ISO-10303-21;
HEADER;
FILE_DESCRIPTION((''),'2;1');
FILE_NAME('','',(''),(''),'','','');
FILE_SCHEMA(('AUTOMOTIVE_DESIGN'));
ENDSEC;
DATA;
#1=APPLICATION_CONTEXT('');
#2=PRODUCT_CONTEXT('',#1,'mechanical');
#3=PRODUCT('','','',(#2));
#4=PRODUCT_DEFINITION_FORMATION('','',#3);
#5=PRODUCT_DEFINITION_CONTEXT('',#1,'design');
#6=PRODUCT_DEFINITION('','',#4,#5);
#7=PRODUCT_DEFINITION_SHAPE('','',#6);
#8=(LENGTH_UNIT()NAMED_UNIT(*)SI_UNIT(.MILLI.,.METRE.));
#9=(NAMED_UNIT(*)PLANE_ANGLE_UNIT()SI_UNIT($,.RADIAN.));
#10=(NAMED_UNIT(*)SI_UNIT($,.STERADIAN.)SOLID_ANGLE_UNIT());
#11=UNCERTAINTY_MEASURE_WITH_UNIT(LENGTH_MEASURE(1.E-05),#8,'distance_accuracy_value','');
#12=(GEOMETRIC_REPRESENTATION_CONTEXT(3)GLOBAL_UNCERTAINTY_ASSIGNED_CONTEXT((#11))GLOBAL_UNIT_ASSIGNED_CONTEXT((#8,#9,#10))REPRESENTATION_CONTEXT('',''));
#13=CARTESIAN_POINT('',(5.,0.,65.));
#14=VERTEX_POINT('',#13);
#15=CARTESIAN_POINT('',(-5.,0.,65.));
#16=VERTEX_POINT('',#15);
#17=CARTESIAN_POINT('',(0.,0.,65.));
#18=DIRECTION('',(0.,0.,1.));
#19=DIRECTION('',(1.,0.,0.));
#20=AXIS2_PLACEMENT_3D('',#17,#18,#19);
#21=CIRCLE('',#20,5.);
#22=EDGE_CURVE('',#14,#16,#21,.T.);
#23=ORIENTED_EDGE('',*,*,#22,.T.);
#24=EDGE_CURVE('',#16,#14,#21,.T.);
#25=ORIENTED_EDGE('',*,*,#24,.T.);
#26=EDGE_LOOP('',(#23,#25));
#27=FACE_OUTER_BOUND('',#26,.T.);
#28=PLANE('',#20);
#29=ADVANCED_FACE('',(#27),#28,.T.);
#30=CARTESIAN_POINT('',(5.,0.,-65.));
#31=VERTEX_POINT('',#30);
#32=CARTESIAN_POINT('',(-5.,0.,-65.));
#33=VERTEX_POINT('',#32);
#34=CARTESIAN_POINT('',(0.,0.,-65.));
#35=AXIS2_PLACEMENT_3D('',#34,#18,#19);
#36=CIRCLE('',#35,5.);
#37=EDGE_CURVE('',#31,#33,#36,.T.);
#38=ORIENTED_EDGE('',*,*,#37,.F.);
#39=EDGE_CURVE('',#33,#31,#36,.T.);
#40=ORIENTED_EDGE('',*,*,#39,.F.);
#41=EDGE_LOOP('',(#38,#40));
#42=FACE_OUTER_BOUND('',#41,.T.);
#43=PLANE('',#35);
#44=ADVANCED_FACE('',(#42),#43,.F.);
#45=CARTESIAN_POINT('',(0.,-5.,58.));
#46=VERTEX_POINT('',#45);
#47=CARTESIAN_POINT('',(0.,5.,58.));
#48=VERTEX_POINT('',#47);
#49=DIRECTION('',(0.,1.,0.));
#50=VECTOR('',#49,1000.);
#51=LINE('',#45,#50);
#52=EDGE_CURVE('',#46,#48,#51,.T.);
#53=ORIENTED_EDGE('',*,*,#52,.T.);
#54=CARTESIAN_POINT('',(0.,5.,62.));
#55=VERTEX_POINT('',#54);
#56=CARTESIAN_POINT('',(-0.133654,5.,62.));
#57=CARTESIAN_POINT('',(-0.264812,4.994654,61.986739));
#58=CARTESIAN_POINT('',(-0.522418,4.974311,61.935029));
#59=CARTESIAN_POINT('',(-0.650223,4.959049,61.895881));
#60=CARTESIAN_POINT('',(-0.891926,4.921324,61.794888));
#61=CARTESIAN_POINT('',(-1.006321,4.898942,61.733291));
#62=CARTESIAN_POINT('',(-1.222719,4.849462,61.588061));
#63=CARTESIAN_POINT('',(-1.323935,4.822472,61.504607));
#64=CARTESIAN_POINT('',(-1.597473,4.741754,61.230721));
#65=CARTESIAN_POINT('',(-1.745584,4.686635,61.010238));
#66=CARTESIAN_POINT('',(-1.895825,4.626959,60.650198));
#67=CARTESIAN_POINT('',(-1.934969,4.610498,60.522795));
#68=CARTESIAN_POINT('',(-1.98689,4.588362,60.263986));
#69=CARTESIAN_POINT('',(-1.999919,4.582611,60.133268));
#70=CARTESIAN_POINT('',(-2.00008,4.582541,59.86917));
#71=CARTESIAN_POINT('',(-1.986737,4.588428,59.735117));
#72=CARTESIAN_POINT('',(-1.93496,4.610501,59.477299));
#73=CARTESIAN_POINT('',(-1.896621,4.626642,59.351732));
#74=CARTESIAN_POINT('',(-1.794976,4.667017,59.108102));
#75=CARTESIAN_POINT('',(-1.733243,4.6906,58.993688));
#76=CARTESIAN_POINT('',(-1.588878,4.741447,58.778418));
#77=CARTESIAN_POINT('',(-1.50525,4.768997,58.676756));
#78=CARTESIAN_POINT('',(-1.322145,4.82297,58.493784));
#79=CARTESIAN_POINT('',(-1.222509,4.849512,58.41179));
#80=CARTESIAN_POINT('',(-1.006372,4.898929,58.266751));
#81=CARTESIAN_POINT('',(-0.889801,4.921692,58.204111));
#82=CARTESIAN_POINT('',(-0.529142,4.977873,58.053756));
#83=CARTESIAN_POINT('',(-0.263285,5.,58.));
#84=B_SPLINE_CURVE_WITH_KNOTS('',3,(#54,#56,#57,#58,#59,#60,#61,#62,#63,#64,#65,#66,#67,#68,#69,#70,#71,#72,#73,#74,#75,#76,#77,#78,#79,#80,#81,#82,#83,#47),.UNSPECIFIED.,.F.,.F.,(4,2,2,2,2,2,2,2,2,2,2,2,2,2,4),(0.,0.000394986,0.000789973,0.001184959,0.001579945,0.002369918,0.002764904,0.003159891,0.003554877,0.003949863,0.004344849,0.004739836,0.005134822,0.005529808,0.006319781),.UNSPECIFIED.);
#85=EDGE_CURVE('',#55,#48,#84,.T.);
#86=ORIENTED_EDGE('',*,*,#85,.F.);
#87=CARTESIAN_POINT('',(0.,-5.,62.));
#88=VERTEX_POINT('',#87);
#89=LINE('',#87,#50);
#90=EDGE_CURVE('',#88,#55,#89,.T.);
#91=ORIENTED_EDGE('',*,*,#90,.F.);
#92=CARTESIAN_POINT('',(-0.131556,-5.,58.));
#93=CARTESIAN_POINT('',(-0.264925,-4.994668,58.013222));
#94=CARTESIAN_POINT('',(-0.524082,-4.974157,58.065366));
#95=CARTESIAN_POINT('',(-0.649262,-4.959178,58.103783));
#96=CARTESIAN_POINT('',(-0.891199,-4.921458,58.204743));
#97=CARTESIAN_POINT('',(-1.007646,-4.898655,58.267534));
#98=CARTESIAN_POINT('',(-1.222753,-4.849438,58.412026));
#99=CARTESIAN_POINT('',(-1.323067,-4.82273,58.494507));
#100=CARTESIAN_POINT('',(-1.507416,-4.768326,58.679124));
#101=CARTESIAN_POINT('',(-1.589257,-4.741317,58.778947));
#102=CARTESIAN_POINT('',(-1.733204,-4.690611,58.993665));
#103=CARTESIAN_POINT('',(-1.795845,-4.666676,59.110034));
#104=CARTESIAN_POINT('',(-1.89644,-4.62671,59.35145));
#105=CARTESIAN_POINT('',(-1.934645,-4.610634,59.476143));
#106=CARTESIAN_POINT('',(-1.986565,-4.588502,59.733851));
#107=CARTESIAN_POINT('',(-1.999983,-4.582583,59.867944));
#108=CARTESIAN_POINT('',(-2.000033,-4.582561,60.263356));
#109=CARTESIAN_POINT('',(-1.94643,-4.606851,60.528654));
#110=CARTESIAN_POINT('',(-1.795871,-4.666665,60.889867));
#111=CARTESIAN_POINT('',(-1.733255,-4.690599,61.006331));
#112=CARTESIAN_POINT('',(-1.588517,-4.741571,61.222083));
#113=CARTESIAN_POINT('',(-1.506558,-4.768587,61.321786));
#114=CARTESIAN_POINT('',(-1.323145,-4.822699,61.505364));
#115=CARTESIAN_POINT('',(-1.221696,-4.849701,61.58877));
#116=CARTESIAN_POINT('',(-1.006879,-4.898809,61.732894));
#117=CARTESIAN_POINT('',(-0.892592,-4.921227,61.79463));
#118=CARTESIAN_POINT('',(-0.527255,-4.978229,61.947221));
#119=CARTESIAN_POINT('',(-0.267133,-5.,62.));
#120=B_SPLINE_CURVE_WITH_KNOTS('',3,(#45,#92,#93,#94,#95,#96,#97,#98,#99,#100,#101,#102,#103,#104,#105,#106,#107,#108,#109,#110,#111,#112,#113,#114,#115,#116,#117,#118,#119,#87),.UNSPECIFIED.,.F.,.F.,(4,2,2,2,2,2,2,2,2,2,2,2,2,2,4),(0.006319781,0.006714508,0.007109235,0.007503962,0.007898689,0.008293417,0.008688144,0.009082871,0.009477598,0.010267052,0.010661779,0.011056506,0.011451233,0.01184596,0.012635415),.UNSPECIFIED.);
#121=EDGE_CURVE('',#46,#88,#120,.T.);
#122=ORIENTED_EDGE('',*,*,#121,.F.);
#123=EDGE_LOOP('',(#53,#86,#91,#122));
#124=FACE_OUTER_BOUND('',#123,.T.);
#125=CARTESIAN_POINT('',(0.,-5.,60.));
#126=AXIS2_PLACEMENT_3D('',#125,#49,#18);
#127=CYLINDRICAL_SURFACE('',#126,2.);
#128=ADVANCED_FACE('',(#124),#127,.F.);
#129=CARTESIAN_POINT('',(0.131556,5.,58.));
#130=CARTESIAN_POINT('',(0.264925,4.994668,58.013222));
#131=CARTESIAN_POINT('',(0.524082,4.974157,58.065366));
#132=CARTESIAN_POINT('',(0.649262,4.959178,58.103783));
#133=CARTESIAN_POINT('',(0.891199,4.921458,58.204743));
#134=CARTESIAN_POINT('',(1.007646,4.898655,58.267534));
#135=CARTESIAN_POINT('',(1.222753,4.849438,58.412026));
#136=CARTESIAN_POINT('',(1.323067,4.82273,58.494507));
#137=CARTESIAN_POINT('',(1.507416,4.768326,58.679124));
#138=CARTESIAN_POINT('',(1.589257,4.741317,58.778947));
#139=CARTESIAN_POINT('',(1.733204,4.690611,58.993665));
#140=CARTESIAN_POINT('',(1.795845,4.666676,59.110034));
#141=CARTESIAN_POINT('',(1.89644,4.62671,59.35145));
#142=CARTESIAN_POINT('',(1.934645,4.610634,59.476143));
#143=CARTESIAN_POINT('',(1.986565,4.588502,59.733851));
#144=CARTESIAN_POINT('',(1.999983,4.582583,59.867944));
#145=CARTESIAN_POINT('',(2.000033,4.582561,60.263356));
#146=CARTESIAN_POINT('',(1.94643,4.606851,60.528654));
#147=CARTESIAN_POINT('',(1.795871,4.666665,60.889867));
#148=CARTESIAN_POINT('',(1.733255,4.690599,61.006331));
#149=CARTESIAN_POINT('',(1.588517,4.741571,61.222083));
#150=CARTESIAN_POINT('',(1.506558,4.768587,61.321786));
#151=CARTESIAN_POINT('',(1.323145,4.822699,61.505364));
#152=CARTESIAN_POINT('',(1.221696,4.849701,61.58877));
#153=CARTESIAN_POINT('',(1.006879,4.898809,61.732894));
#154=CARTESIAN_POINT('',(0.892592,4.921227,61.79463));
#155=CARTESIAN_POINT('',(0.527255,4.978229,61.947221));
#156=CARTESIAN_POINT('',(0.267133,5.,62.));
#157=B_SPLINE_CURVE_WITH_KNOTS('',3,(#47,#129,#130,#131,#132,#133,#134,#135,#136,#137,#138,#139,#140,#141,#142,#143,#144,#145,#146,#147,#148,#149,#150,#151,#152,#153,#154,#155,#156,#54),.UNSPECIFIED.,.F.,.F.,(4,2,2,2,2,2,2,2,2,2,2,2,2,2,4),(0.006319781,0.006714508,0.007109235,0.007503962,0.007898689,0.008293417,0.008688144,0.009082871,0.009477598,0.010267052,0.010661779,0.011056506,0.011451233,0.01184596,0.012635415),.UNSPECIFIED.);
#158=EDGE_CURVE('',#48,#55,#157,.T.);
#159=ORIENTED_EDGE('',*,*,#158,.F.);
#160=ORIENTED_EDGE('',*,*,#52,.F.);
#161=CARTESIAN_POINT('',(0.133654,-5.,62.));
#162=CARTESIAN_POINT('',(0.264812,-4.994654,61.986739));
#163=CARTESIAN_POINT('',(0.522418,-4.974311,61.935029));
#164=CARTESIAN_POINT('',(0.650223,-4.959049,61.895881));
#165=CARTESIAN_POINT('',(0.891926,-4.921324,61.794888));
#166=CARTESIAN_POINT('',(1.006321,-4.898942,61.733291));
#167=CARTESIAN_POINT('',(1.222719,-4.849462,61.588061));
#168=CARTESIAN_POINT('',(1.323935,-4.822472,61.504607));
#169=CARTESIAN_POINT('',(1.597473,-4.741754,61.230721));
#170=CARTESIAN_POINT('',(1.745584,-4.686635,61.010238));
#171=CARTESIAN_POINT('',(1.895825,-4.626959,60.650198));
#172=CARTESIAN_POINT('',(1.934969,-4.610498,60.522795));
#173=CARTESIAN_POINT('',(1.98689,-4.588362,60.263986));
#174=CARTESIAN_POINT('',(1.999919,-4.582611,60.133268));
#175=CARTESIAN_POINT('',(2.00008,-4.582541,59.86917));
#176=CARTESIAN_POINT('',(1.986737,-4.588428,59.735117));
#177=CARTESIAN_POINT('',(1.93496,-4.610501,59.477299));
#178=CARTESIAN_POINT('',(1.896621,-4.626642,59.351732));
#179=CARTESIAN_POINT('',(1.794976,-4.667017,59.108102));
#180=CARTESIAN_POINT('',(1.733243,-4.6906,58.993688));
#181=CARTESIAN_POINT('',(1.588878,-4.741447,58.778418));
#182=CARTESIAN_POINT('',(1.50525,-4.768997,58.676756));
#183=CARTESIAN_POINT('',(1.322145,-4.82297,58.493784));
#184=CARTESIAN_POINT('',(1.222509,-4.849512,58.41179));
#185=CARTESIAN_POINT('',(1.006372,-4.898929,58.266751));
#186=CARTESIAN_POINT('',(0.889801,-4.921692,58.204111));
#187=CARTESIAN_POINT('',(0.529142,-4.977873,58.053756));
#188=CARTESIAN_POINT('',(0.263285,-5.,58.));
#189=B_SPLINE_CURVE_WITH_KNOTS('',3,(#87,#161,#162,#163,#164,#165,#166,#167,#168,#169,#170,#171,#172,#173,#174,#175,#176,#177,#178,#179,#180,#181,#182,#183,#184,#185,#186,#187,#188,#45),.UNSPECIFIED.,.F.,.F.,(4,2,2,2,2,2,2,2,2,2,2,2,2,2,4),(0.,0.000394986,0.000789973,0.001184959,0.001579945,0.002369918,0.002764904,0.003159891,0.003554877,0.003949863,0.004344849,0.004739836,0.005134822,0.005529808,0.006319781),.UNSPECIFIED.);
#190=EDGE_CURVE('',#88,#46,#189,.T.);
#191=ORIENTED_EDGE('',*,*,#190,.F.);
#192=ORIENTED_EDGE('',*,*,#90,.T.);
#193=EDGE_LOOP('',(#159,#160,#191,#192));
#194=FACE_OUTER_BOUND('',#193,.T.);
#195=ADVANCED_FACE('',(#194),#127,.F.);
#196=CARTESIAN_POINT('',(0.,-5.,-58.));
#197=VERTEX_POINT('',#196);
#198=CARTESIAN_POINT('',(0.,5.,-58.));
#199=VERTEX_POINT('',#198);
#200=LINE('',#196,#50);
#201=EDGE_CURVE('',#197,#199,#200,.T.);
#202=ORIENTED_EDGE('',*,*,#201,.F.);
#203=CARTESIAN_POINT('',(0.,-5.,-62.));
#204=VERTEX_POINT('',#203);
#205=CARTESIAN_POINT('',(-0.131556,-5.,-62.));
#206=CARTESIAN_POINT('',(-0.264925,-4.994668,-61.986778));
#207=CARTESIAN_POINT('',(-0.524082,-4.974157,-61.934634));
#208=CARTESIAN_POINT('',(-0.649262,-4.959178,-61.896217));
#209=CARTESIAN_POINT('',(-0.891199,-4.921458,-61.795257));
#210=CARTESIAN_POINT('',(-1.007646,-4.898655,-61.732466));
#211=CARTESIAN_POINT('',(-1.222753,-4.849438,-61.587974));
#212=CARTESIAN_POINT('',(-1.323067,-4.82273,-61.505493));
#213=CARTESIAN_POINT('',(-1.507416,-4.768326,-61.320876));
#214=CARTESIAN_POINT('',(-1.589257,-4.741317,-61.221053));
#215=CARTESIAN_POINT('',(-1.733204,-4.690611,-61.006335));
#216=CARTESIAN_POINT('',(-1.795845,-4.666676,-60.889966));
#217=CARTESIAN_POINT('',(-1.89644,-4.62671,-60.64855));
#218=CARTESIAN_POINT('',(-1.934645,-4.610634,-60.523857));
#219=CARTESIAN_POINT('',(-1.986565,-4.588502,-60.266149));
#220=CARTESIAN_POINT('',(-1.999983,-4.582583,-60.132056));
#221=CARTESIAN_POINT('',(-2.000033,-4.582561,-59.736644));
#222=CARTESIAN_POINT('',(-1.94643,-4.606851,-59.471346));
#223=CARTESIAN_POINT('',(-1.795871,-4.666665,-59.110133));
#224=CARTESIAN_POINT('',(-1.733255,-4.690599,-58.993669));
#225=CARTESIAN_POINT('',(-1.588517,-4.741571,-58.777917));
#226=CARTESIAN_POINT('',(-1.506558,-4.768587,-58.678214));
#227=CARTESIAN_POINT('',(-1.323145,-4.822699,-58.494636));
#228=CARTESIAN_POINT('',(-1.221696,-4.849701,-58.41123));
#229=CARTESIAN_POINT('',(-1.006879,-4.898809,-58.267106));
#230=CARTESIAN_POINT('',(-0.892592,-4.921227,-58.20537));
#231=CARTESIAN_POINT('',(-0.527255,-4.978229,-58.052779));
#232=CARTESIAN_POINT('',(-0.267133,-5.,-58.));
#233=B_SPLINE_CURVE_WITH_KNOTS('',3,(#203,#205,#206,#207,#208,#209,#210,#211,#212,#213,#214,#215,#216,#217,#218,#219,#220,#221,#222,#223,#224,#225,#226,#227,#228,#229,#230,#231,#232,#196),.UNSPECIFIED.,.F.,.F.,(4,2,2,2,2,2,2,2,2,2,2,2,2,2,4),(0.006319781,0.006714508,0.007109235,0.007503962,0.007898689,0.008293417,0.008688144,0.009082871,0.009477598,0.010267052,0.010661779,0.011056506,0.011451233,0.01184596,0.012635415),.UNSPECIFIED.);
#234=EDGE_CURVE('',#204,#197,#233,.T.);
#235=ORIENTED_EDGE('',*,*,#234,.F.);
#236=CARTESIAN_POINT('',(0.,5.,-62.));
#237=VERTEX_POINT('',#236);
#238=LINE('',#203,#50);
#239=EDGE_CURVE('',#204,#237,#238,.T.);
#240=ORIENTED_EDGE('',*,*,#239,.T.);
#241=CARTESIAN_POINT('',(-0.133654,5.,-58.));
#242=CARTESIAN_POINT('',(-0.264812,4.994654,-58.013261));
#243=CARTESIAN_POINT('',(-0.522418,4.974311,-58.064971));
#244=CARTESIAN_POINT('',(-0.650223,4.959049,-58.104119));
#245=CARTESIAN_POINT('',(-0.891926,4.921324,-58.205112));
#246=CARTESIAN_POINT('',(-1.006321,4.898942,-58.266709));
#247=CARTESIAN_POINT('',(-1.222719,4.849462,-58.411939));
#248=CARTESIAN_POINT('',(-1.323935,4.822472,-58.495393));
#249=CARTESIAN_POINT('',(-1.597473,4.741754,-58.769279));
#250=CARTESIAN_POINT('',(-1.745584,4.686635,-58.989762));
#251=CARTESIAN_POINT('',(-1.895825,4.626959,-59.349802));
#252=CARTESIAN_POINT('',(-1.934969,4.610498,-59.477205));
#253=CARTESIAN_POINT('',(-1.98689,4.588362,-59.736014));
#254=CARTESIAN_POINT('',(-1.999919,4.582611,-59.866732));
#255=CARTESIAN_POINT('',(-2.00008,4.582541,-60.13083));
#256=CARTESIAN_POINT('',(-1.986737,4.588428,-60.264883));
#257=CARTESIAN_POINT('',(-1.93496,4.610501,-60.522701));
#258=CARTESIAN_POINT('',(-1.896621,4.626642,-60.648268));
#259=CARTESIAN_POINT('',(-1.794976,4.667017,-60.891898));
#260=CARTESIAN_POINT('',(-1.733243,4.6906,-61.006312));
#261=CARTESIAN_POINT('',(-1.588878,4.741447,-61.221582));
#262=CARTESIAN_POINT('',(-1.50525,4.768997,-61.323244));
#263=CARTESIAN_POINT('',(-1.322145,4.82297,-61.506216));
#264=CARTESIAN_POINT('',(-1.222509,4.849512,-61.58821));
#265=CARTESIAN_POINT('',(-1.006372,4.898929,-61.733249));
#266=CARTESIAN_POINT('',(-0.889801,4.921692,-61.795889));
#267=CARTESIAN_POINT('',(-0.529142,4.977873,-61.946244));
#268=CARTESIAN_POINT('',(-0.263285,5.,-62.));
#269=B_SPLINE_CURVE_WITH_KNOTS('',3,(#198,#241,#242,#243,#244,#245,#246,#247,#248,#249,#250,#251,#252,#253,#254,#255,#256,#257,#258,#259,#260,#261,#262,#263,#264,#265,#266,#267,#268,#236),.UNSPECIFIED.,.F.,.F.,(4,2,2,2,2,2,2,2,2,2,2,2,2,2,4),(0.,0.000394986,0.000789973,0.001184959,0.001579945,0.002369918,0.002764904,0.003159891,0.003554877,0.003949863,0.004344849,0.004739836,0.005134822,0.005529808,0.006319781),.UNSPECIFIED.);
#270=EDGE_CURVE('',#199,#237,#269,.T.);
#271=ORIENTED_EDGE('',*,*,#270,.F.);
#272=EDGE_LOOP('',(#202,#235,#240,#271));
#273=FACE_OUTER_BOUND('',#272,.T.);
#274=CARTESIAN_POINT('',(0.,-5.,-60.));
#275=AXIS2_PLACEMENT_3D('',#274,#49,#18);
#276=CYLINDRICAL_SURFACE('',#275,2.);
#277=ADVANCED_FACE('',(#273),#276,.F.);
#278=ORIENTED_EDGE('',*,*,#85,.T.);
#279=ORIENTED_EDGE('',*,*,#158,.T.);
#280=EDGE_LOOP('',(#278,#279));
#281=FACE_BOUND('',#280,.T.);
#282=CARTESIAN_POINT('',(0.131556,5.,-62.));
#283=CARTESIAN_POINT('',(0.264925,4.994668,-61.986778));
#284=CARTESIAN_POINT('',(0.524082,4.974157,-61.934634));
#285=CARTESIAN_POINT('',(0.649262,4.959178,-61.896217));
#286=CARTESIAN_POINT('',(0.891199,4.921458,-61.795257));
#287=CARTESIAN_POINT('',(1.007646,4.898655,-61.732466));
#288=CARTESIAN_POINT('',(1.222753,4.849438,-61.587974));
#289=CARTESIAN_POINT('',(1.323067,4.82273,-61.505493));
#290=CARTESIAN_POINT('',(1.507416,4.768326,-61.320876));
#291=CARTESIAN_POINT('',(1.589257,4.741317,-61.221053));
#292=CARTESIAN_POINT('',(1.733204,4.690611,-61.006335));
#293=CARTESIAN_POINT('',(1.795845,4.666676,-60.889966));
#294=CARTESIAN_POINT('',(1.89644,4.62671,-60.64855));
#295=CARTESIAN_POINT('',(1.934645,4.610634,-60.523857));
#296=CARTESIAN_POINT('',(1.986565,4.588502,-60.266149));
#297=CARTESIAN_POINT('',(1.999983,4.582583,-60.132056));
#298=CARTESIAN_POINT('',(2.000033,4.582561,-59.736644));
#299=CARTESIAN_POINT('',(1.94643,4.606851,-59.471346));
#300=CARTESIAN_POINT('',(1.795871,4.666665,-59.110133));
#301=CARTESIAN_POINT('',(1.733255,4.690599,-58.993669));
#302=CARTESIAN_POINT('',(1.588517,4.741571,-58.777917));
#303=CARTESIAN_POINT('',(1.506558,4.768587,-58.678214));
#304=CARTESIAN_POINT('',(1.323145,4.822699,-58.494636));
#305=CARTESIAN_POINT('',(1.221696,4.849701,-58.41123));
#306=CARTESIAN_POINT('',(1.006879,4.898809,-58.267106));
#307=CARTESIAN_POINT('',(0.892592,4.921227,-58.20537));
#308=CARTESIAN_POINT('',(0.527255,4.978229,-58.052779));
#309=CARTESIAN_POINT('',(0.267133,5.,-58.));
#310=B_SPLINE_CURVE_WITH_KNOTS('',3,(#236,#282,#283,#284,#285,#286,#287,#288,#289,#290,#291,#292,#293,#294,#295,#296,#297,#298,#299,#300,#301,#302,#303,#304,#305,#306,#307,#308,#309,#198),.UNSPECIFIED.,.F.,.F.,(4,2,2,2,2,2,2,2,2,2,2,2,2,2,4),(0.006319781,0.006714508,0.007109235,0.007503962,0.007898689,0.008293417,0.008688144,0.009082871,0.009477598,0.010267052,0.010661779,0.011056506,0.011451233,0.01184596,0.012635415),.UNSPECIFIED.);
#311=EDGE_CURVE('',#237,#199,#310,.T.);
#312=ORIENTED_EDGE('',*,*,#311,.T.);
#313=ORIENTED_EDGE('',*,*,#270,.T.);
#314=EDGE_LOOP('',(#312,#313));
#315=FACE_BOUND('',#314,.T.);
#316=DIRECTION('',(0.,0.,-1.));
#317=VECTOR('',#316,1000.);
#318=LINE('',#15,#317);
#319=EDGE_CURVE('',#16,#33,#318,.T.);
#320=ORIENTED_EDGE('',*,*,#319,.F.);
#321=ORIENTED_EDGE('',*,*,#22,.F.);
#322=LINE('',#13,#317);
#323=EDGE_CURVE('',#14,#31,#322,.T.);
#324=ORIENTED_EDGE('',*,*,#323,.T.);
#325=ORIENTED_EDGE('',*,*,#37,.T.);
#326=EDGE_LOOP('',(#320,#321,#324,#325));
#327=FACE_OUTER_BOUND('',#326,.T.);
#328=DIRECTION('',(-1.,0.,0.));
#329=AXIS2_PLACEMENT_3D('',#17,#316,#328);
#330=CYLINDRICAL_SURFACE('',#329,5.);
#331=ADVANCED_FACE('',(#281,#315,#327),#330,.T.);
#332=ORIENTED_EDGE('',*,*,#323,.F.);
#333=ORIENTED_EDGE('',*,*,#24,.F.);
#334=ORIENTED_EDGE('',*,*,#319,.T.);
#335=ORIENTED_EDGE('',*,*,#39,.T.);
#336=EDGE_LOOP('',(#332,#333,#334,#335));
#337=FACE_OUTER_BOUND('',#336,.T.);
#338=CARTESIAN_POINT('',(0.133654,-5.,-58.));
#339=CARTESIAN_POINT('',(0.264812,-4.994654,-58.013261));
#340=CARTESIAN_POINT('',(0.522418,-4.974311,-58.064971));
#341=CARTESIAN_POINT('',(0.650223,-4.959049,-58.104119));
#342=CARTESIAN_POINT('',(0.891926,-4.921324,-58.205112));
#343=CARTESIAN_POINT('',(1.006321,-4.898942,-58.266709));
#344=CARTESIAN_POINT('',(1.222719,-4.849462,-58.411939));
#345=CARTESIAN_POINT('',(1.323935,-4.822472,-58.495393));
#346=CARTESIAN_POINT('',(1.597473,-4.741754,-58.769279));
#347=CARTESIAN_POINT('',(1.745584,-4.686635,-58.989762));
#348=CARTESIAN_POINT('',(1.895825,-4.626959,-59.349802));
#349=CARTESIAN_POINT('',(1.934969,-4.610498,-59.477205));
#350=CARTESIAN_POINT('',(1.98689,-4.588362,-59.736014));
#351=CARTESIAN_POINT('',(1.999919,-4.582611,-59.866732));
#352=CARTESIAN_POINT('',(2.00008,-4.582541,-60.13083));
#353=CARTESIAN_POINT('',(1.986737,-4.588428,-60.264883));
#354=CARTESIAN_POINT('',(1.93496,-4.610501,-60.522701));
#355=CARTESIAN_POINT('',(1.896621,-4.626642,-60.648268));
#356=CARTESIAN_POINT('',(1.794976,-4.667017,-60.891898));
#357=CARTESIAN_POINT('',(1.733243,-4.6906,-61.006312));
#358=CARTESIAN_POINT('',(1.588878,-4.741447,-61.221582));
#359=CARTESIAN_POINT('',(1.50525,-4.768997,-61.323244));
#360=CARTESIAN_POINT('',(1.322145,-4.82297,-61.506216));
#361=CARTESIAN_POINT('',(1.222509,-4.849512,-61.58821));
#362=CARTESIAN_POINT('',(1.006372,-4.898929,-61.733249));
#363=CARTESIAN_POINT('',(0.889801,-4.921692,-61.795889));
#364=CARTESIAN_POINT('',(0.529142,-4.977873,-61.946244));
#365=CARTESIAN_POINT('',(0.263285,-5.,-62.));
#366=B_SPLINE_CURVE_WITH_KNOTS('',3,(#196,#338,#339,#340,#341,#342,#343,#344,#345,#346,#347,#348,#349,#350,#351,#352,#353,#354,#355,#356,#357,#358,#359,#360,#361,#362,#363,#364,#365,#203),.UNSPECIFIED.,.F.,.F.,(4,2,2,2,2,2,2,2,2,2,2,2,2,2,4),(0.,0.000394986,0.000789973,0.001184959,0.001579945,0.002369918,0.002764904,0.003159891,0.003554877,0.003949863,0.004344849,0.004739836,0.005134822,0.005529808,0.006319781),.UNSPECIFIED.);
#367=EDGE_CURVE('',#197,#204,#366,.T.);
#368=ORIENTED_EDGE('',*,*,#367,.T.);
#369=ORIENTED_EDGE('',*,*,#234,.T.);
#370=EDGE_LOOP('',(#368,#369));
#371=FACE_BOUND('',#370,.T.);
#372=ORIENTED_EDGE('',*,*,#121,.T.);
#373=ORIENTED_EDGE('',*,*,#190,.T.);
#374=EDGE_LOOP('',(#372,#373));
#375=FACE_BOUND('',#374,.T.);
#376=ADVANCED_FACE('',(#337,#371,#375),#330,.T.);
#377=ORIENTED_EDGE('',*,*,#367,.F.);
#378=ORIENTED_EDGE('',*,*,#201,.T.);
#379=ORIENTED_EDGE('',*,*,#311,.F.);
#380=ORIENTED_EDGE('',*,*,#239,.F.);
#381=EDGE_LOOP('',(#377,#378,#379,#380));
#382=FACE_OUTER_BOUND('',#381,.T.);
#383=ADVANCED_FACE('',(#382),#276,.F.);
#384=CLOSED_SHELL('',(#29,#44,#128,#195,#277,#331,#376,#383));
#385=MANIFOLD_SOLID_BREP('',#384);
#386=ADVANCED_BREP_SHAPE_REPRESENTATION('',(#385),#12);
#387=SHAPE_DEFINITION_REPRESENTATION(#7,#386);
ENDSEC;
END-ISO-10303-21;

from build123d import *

# Parameters (mm, degrees)
SKETCH_1_R          = 5
EXTRUDE_1_DEPTH     = 65
SKETCH_2_R          = 2
CUT_EXTRUDE_1_DEPTH = 10


with BuildPart() as part:
    # 草图1 → 凸台-拉伸1 (new, symmetric)
    with BuildSketch(Plane.XY):
        Circle(SKETCH_1_R)
    extrude(amount=EXTRUDE_1_DEPTH, both=True)

    # 草图2 → 切除-拉伸1 (cut)
    with BuildSketch(Plane(origin=(0, 5, 0), x_dir=(1, 0, 0), z_dir=(0, 1, 0))):
        with Locations(Location((0, -60, 0), (0, 0, 270))):
            Circle(SKETCH_2_R)
        with Locations(Location((0, 60, 0), (0, 0, 270))):
            Circle(SKETCH_2_R)
    extrude(amount=-CUT_EXTRUDE_1_DEPTH, mode=Mode.SUBTRACT)


solid = part.part
